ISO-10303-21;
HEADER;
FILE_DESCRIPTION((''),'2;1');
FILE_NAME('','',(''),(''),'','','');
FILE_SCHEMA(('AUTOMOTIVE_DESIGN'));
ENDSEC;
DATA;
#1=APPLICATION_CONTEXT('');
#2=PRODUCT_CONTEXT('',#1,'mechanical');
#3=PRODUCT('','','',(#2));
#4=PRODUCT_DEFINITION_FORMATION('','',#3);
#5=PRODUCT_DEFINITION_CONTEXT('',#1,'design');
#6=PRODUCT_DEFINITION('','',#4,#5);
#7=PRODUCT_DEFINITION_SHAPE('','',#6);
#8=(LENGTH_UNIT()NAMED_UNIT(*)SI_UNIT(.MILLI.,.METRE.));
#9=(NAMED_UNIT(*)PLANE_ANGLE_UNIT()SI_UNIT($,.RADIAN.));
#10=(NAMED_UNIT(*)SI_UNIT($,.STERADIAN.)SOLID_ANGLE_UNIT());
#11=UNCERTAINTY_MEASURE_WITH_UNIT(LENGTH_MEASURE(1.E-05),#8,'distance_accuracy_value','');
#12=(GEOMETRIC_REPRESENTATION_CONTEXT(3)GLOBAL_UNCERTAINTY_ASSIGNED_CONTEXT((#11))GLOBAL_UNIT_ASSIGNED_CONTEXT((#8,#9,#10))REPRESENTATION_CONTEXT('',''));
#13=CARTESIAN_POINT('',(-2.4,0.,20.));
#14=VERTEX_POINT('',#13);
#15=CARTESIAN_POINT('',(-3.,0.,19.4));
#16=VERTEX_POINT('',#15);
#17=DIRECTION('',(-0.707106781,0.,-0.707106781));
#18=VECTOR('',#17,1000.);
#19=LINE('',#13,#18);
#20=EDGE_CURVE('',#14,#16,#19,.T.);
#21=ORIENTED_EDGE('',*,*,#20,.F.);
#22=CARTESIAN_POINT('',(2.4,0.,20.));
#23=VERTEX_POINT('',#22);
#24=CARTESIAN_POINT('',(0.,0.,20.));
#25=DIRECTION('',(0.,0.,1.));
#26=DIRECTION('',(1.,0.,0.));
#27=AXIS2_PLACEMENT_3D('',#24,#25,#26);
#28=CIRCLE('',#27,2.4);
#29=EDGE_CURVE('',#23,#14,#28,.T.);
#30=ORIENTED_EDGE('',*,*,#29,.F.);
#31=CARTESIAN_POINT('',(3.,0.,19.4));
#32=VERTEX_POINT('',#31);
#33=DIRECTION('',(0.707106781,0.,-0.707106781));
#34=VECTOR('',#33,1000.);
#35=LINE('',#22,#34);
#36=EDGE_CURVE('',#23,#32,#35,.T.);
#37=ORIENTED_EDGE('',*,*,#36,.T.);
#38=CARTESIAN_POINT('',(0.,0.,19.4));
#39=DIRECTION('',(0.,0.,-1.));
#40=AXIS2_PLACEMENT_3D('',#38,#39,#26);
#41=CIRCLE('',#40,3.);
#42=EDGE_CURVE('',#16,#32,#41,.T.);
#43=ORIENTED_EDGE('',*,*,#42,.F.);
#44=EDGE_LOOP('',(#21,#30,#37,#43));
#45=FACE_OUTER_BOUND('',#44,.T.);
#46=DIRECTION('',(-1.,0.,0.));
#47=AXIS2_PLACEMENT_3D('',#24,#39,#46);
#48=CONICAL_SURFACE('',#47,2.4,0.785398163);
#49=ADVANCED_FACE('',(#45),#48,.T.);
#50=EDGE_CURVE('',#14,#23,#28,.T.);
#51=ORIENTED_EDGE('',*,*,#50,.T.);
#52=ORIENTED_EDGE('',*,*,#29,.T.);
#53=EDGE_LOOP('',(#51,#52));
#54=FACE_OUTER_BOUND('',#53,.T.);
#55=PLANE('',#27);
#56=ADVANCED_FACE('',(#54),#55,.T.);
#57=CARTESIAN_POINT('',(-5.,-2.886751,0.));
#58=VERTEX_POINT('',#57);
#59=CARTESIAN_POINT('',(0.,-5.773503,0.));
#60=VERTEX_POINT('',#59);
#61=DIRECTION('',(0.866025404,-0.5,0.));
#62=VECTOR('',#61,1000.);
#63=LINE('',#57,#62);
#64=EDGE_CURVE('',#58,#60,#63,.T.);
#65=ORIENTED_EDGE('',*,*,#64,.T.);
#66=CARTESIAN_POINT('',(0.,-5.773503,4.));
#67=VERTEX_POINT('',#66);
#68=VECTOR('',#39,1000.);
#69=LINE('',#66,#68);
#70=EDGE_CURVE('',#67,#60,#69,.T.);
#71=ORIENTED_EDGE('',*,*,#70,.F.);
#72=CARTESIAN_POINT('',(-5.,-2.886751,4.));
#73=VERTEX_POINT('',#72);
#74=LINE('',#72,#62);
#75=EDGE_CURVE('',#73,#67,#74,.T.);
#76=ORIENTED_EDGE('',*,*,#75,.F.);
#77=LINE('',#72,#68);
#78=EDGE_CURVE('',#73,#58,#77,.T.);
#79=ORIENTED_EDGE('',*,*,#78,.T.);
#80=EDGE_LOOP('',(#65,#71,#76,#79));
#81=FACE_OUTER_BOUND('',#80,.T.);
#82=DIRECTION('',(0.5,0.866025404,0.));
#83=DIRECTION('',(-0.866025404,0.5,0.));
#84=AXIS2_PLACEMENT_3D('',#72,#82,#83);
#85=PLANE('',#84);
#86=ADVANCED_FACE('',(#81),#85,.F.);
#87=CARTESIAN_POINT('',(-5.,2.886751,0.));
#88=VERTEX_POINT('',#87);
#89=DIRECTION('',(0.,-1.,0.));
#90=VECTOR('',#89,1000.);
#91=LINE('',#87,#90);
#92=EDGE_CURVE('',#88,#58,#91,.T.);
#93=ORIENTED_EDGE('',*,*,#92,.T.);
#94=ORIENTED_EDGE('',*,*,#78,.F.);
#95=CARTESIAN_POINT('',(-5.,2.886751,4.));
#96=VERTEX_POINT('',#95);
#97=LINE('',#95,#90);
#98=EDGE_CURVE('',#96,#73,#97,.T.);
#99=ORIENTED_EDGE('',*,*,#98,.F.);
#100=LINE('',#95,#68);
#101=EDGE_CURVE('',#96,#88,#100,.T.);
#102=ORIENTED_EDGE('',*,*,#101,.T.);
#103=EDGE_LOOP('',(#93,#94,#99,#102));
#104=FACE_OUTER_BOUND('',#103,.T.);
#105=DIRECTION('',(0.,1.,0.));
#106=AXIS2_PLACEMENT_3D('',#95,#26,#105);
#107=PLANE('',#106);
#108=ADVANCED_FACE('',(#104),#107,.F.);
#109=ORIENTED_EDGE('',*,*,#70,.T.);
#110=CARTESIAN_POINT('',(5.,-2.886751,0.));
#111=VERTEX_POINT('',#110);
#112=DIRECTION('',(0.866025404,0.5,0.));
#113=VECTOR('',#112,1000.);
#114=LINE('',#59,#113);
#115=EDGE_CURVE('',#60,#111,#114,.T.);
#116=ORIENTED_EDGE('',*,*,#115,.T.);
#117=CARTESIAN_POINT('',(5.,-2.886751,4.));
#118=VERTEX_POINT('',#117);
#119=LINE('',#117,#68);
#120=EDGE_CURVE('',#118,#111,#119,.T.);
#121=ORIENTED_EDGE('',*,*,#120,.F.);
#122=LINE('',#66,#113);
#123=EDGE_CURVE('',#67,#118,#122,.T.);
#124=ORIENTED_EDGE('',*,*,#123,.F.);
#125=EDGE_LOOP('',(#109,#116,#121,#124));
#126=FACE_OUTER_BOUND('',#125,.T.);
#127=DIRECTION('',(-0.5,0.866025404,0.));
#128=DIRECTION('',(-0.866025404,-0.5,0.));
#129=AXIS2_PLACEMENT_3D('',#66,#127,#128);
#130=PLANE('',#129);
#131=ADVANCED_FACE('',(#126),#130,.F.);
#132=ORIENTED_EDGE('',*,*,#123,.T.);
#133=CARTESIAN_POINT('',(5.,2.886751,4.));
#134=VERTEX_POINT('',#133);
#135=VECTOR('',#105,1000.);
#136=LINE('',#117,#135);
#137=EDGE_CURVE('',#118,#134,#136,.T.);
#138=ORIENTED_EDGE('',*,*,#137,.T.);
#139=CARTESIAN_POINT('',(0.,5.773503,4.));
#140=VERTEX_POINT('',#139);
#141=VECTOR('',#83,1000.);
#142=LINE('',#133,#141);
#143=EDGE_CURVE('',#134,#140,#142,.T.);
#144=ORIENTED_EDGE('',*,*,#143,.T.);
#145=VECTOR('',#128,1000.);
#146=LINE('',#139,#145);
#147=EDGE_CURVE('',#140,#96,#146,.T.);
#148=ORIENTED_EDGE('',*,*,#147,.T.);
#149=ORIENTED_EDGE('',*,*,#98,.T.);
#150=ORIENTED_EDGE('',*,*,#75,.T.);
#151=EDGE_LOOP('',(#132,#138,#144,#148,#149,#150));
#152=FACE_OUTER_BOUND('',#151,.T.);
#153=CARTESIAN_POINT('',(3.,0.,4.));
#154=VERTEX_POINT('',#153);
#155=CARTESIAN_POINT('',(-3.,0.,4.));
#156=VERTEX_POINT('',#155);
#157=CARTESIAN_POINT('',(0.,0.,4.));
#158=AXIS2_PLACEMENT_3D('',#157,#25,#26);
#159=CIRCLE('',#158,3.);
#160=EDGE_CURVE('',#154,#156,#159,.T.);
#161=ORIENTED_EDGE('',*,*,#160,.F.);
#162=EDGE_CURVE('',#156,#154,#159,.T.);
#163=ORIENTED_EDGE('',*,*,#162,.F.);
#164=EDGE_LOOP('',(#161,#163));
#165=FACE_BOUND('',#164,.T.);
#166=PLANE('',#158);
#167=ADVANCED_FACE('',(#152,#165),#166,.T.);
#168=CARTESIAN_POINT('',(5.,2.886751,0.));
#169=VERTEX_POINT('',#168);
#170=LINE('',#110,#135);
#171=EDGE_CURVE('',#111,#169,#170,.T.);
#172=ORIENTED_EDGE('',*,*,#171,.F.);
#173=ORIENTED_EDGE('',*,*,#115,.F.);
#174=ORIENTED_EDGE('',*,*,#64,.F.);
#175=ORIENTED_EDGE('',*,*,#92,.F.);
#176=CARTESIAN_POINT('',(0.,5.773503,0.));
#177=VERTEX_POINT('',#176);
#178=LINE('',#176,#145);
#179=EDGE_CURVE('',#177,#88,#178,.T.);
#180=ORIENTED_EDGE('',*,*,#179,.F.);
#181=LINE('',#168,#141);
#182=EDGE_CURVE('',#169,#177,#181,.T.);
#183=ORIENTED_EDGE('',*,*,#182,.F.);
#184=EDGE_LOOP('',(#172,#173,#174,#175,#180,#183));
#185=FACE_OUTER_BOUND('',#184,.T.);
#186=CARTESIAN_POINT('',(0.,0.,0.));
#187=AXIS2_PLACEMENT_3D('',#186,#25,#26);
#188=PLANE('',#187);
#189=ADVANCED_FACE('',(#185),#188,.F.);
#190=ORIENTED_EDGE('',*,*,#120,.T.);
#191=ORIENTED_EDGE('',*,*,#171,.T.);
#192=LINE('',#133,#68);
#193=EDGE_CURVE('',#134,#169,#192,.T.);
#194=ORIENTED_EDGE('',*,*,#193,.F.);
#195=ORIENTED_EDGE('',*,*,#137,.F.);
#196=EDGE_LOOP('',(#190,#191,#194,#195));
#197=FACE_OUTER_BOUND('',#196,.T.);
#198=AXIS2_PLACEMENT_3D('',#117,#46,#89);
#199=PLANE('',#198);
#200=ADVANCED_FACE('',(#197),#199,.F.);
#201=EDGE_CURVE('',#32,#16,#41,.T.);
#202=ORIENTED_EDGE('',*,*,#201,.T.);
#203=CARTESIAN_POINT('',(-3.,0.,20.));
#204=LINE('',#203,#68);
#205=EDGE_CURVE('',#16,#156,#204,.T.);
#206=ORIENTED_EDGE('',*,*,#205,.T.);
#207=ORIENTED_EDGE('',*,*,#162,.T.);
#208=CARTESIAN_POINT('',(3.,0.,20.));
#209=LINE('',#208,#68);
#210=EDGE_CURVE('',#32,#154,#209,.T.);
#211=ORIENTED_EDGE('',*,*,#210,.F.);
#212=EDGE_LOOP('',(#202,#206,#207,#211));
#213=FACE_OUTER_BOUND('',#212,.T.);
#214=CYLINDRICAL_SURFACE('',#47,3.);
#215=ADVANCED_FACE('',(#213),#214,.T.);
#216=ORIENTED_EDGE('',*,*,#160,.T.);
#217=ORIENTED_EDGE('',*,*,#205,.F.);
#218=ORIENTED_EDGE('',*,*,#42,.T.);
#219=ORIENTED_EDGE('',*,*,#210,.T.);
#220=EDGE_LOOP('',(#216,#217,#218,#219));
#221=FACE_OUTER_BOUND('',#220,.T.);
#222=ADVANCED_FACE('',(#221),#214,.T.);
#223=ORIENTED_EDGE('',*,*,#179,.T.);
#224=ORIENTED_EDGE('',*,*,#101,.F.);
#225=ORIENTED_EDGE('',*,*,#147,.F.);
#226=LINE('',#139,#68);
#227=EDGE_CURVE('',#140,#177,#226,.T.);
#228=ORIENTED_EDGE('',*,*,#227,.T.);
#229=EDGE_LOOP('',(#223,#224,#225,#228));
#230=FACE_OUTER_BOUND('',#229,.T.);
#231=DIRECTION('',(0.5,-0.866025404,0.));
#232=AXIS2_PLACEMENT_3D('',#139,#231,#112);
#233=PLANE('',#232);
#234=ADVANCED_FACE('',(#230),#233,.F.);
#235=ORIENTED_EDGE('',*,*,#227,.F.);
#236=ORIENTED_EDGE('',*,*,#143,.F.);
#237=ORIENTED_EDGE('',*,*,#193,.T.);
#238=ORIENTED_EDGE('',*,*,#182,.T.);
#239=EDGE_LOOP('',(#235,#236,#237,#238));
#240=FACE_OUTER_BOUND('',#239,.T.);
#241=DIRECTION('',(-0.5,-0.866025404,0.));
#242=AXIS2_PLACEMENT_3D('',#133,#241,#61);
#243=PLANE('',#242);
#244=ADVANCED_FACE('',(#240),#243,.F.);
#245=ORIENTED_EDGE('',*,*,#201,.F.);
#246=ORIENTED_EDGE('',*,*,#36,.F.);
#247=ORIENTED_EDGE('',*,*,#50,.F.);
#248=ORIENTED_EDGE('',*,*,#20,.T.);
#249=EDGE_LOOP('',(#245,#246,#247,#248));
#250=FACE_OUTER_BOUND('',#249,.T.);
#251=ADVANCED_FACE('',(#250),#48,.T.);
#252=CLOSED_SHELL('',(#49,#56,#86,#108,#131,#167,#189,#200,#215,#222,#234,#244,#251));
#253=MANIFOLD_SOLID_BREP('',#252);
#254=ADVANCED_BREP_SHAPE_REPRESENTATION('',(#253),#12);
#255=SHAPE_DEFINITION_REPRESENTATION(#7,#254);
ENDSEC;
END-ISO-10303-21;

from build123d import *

# Parameters (mm, degrees)
BOSS_EXTRUDE1_DEPTH = 4
SKETCH3_R           = 3
BOSS_EXTRUDE2_DEPTH = 16
CHAMFER1_SIZE       = 0.6


with BuildPart() as part:
    # Sketch1 → Boss-Extrude1 (new body)
    with BuildSketch(Plane.XY):
        Polygon((5, 2.886751346), (0, 5.773502692), (-5, 2.886751346), (-5, -2.886751346), (0, -5.773502692), (5, -2.886751346), align=None)
    extrude(amount=BOSS_EXTRUDE1_DEPTH)

    # Sketch3 → Boss-Extrude2 (add)
    with BuildSketch(Plane.XY.offset(4)):
        Circle(SKETCH3_R)
    extrude(amount=BOSS_EXTRUDE2_DEPTH)

    # Chamfer1
    chamfer1_edges = [part.edges().sort_by_distance(p)[0] for p in [
        (-3, 0, 20),
    ]]
    chamfer(chamfer1_edges, length=CHAMFER1_SIZE)


solid = part.part
